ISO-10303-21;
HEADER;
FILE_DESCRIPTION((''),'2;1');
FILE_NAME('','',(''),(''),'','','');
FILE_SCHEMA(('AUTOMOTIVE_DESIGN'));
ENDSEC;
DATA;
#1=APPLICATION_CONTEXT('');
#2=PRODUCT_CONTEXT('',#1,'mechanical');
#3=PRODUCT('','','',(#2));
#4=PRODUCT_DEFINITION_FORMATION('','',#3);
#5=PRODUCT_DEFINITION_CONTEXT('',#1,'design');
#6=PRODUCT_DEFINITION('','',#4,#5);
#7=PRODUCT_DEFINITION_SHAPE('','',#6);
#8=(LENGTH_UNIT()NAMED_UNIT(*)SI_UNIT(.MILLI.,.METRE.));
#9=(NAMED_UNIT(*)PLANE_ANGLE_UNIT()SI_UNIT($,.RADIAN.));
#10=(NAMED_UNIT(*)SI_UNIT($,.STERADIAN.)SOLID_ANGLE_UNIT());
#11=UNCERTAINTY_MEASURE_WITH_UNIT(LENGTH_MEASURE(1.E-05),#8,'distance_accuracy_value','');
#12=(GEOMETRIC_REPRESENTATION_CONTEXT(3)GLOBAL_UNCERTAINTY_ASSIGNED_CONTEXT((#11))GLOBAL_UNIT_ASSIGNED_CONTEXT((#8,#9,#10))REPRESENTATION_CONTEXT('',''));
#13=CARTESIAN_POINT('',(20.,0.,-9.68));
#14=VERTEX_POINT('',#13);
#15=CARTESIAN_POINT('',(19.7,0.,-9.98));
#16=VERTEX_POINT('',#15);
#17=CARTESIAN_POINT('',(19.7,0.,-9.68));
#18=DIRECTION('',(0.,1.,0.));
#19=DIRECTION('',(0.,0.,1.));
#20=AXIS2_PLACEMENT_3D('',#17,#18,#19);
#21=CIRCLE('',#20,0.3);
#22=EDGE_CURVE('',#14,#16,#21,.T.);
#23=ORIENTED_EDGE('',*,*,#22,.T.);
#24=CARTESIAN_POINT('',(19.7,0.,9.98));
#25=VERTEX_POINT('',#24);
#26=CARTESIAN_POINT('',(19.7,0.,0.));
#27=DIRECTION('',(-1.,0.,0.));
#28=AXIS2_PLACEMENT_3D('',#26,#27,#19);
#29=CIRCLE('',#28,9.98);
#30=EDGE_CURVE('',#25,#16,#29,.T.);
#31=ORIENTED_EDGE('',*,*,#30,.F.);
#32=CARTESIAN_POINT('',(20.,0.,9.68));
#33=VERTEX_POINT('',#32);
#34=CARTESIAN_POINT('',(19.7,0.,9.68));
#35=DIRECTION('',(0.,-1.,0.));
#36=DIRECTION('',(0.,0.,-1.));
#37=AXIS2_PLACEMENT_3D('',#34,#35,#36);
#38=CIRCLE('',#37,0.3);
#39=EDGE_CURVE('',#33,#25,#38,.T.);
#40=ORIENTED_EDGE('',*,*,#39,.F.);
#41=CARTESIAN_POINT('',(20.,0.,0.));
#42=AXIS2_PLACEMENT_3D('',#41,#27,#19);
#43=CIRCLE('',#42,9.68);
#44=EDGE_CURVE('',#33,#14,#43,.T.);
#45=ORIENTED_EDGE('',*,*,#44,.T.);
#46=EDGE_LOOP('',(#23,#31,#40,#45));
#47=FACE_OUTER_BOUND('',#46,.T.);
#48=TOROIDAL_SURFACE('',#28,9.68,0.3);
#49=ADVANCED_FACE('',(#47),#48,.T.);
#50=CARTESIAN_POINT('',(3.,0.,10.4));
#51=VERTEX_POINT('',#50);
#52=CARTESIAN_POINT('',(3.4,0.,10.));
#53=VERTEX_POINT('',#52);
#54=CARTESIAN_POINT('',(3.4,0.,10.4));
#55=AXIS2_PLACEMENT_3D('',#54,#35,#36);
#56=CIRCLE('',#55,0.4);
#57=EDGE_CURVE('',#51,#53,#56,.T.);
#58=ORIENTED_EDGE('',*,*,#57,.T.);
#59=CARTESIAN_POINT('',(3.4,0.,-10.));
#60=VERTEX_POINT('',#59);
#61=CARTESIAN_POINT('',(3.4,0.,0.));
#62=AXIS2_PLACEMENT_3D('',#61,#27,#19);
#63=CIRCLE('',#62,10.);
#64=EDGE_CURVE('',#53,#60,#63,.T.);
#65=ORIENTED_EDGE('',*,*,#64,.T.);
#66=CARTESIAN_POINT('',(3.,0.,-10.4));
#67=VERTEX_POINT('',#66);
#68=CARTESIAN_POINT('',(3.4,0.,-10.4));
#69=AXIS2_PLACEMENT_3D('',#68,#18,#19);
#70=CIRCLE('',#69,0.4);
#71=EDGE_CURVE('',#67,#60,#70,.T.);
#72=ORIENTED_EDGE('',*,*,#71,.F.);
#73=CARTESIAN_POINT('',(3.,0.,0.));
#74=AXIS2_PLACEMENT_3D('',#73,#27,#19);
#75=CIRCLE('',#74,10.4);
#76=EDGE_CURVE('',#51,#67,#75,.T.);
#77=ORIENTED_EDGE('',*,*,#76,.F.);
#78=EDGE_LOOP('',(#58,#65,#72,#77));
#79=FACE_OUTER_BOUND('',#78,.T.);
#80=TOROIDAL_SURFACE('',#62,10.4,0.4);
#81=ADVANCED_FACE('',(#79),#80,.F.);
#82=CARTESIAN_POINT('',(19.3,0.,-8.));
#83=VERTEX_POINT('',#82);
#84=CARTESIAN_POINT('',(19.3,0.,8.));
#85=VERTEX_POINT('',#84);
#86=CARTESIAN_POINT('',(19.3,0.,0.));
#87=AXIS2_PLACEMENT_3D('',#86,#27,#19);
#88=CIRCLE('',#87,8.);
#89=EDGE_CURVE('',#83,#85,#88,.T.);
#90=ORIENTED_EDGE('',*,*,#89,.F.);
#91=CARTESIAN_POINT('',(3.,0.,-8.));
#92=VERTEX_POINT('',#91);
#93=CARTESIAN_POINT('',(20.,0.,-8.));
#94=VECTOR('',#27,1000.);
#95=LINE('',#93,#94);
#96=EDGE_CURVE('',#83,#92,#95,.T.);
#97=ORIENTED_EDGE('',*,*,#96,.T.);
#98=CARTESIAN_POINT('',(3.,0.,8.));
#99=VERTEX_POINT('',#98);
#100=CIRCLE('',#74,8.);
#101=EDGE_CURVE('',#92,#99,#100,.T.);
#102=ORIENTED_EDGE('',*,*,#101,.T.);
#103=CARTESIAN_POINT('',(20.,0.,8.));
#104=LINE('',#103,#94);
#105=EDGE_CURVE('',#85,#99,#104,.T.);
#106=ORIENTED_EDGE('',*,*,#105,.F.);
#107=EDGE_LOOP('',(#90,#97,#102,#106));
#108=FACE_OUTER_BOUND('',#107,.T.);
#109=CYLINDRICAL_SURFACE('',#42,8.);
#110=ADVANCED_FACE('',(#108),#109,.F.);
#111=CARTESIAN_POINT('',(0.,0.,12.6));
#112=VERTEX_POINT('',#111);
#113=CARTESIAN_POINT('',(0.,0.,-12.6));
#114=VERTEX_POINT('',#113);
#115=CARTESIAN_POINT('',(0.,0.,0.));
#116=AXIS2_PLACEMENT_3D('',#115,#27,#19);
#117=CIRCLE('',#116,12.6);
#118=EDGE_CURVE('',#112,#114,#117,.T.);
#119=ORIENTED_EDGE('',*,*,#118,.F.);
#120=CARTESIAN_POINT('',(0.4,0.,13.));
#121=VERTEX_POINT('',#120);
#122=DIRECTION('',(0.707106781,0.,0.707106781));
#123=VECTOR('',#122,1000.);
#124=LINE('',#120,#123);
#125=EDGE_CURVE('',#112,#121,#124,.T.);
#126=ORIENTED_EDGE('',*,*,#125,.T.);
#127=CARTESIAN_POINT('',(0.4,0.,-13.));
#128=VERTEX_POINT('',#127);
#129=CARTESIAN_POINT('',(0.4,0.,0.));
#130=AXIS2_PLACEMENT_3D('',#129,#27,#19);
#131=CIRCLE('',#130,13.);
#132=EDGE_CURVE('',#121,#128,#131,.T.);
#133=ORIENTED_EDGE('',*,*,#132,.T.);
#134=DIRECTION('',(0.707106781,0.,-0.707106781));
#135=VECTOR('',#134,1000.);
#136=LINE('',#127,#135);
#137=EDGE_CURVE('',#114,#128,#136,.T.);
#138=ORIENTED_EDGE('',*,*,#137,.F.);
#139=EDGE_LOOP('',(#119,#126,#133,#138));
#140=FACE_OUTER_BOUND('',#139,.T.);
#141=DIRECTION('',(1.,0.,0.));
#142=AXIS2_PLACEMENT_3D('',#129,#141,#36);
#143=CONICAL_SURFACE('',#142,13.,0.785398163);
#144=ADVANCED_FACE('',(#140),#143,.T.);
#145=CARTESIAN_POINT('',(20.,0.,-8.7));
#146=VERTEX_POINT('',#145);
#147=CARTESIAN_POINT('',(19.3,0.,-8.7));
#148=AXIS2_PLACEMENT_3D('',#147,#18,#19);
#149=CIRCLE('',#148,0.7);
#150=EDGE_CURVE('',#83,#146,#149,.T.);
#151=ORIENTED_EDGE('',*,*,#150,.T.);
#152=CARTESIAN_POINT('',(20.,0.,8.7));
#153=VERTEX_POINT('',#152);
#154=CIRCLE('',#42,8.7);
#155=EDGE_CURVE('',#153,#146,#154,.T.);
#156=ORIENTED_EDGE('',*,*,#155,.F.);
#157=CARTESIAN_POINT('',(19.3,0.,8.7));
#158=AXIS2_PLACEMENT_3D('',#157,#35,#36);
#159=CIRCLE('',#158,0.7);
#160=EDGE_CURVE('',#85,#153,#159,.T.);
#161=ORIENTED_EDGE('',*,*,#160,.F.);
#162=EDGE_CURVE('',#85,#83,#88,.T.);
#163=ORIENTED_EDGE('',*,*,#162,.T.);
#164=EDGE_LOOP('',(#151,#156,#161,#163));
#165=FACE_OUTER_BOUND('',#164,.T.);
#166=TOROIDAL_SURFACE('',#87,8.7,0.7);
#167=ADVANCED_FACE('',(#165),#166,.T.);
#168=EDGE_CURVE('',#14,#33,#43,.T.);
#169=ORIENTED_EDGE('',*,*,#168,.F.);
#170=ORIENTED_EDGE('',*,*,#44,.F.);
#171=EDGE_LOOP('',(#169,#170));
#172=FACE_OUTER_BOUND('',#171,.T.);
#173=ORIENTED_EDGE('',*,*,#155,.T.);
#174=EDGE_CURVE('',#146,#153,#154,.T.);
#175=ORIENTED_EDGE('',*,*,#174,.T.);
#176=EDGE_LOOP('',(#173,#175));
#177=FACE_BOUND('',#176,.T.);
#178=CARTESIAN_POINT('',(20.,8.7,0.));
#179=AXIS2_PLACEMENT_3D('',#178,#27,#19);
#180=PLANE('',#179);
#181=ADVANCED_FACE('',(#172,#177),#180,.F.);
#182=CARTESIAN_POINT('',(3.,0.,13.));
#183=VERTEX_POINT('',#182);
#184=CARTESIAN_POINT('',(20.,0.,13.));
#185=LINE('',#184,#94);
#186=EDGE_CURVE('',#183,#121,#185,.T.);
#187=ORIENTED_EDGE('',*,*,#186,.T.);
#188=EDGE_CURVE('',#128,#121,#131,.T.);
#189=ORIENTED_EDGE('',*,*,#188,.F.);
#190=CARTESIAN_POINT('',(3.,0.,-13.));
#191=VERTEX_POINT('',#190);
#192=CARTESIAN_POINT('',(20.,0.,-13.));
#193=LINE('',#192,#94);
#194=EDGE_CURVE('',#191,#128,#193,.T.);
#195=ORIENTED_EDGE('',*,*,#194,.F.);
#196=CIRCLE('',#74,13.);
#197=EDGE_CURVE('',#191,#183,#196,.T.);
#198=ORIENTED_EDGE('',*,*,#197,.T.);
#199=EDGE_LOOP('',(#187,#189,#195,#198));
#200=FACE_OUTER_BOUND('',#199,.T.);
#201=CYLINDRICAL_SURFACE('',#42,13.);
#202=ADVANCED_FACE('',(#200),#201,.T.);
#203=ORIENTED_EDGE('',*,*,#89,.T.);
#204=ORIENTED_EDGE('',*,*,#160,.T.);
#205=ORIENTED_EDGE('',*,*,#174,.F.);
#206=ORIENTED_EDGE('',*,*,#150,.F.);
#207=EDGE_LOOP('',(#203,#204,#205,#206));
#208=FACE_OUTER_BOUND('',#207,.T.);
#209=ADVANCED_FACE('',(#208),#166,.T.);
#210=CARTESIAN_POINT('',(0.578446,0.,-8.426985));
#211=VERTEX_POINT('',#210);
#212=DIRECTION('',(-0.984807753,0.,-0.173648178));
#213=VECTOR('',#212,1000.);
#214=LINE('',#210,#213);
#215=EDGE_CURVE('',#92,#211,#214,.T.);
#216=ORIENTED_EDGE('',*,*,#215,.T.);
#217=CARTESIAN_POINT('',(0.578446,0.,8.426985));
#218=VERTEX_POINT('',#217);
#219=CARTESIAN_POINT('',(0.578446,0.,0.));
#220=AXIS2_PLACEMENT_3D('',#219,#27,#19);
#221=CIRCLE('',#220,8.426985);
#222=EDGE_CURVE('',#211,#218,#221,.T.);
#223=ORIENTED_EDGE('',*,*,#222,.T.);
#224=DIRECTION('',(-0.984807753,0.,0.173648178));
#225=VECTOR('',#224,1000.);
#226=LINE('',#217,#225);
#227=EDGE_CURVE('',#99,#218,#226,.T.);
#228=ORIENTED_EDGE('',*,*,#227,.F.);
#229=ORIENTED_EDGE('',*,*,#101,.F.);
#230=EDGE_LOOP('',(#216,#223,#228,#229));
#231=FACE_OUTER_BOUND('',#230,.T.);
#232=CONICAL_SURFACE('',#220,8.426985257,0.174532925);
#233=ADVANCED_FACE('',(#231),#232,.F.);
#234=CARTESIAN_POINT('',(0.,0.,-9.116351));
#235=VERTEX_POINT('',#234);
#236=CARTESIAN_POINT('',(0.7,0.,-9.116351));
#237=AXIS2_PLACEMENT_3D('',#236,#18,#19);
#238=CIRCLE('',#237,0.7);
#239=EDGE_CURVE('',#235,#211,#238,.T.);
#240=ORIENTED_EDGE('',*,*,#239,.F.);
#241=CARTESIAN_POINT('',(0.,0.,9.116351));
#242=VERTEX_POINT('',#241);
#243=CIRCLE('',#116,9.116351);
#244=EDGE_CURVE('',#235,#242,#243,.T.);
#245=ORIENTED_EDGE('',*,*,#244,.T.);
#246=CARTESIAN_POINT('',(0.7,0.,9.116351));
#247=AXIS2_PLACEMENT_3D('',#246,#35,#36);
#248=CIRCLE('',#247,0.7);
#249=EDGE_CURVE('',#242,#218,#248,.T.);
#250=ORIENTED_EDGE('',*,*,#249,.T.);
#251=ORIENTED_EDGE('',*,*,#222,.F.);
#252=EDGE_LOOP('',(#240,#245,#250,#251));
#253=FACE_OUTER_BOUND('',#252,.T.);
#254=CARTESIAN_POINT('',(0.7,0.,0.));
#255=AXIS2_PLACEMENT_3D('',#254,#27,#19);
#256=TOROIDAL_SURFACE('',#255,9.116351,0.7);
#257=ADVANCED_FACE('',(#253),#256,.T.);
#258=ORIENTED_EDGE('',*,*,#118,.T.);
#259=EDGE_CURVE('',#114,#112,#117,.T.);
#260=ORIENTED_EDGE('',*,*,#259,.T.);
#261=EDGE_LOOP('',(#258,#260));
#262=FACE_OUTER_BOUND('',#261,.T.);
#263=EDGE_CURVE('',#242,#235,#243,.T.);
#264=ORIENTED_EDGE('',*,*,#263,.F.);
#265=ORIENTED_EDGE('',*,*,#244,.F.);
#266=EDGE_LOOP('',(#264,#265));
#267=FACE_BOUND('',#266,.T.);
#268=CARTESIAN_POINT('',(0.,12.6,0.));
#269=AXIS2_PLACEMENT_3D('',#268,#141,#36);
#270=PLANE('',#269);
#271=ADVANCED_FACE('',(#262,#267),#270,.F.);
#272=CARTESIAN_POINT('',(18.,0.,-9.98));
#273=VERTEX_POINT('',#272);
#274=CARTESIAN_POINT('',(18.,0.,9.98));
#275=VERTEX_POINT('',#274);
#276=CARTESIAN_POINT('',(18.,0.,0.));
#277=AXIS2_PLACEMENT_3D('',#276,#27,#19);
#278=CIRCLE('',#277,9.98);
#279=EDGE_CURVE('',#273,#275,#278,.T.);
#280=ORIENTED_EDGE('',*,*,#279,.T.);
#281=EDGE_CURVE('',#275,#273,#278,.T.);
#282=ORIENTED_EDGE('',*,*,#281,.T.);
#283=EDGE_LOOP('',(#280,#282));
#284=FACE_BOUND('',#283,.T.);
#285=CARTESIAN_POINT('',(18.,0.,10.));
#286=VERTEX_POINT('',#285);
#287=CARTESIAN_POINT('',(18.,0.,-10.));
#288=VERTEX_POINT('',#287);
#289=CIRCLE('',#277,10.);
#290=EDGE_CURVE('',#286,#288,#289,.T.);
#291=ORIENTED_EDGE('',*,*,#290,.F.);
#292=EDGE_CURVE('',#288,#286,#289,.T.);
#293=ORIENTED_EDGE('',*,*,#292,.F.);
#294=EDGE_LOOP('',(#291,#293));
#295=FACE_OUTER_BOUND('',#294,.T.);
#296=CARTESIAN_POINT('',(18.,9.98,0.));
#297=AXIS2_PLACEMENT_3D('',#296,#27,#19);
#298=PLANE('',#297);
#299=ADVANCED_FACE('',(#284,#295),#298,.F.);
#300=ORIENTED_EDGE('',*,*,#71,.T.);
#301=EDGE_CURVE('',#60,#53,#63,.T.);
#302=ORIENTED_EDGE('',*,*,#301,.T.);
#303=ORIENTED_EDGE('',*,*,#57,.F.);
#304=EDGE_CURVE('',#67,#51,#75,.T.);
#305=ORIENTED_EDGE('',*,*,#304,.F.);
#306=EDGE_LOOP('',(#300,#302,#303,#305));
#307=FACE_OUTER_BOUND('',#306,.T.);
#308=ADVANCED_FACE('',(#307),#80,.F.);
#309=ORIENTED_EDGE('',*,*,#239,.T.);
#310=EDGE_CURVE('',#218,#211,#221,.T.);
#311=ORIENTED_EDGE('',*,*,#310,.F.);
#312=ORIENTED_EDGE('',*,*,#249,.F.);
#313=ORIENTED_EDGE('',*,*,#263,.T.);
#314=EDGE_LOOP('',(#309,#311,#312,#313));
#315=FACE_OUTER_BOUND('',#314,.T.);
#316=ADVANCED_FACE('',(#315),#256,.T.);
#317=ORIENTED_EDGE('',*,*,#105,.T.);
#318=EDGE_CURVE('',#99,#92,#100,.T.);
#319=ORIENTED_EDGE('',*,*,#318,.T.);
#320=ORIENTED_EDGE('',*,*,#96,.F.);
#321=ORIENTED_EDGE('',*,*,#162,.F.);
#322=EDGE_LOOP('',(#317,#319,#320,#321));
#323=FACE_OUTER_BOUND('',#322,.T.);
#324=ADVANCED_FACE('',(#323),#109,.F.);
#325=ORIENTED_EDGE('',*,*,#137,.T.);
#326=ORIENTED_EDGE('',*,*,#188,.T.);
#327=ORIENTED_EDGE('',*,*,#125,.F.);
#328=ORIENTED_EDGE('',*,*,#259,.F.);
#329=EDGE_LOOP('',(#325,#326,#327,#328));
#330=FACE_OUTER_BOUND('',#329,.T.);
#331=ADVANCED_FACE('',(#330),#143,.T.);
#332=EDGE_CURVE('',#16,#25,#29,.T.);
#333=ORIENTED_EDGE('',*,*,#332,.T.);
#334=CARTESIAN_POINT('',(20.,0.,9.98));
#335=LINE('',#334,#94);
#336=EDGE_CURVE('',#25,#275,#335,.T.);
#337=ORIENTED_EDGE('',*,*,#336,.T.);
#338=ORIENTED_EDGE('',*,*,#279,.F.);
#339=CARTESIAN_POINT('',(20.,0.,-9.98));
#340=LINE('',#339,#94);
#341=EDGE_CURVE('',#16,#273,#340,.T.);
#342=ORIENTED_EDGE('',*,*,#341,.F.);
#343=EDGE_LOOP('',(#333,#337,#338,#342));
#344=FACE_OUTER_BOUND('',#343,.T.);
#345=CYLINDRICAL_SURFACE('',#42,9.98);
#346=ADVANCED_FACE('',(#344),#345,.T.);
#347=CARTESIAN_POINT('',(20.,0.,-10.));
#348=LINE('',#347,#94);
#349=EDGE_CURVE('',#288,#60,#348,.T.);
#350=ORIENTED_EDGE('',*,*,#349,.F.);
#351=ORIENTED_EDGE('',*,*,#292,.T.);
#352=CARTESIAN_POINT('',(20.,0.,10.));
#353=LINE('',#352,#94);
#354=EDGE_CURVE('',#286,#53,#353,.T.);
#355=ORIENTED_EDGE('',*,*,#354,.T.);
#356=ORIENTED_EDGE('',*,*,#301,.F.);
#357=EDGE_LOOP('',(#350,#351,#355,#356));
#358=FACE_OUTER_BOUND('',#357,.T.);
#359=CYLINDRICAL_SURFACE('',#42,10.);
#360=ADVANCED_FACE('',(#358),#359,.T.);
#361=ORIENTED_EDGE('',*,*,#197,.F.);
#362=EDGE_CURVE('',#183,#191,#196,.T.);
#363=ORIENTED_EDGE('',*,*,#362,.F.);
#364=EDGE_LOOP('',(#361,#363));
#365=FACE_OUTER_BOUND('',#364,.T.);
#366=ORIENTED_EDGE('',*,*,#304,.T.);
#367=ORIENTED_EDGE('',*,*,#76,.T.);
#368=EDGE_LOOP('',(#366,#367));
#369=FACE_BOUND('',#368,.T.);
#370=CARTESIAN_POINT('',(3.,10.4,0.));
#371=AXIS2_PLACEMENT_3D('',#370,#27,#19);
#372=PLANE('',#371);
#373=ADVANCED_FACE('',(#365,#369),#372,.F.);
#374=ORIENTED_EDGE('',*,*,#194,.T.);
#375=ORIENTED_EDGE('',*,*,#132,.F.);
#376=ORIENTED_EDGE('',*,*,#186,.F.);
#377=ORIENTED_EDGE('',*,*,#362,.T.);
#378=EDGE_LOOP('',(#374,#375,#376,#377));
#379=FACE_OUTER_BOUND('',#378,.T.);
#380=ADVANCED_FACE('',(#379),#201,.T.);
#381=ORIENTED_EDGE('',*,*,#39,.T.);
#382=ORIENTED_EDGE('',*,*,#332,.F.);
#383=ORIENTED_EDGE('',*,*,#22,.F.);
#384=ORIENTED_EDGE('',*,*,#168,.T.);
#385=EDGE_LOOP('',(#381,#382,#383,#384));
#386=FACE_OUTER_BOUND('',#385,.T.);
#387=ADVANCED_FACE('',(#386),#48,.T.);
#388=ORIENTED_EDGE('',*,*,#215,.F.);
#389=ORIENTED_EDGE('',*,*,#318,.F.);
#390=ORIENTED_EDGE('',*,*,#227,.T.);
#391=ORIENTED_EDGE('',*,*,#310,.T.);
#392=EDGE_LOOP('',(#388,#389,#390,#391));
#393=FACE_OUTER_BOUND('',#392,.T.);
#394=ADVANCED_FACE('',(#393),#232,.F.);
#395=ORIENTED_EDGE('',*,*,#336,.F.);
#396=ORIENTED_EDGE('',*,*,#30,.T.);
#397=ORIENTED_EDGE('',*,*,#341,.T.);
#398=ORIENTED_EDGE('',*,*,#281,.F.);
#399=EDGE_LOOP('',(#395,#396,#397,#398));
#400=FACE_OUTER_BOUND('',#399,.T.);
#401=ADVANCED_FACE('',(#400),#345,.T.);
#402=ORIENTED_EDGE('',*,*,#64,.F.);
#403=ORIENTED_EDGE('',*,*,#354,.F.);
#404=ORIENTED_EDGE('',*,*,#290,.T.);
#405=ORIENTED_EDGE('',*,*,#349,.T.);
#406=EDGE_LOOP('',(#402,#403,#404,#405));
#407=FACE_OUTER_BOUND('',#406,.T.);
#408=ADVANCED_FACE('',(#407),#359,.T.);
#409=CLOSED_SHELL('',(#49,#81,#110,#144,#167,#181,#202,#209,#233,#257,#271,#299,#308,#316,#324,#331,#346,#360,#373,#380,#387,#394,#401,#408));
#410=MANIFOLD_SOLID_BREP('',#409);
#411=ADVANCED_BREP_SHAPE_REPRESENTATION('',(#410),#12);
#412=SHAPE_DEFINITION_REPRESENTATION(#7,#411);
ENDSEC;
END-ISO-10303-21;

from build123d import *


with BuildPart() as part:
    # Sketch1 → Revolve1 (revolve)
    with BuildSketch(Plane.XY, mode=Mode.PRIVATE) as revolve1_sk:
        with BuildLine():
            Line((0, 12.6), (0, 9.116350684))
            ThreePointArc((0, 9.116350684), (0.16376889, 8.666399357), (0.578446276, 8.426985257))
            Line((0.578446276, 8.426985257), (3, 8))
            Line((3, 8), (19.3, 8))
            ThreePointArc((19.3, 8), (19.794974747, 8.205025253), (20, 8.7))
            Line((20, 8.7), (20, 9.68))
            ThreePointArc((20, 9.68), (19.912132034, 9.892132034), (19.7, 9.98))
            Line((19.7, 9.98), (18, 9.98))
            Line((18, 9.98), (18, 10))
            Line((18, 10), (3.4, 10))
            ThreePointArc((3.4, 10), (3.117157288, 10.117157288), (3, 10.4))
            Line((3, 10.4), (3, 13))
            Line((3, 13), (0.4, 13))
            Line((0.4, 13), (0, 12.6))
        make_face()
    revolve(revolve1_sk.sketch.rotate(Axis((20, 0, 0), (-1, 0, 0)), 270), axis=Axis((20, 0, 0), (-1, 0, 0)))


solid = part.part
